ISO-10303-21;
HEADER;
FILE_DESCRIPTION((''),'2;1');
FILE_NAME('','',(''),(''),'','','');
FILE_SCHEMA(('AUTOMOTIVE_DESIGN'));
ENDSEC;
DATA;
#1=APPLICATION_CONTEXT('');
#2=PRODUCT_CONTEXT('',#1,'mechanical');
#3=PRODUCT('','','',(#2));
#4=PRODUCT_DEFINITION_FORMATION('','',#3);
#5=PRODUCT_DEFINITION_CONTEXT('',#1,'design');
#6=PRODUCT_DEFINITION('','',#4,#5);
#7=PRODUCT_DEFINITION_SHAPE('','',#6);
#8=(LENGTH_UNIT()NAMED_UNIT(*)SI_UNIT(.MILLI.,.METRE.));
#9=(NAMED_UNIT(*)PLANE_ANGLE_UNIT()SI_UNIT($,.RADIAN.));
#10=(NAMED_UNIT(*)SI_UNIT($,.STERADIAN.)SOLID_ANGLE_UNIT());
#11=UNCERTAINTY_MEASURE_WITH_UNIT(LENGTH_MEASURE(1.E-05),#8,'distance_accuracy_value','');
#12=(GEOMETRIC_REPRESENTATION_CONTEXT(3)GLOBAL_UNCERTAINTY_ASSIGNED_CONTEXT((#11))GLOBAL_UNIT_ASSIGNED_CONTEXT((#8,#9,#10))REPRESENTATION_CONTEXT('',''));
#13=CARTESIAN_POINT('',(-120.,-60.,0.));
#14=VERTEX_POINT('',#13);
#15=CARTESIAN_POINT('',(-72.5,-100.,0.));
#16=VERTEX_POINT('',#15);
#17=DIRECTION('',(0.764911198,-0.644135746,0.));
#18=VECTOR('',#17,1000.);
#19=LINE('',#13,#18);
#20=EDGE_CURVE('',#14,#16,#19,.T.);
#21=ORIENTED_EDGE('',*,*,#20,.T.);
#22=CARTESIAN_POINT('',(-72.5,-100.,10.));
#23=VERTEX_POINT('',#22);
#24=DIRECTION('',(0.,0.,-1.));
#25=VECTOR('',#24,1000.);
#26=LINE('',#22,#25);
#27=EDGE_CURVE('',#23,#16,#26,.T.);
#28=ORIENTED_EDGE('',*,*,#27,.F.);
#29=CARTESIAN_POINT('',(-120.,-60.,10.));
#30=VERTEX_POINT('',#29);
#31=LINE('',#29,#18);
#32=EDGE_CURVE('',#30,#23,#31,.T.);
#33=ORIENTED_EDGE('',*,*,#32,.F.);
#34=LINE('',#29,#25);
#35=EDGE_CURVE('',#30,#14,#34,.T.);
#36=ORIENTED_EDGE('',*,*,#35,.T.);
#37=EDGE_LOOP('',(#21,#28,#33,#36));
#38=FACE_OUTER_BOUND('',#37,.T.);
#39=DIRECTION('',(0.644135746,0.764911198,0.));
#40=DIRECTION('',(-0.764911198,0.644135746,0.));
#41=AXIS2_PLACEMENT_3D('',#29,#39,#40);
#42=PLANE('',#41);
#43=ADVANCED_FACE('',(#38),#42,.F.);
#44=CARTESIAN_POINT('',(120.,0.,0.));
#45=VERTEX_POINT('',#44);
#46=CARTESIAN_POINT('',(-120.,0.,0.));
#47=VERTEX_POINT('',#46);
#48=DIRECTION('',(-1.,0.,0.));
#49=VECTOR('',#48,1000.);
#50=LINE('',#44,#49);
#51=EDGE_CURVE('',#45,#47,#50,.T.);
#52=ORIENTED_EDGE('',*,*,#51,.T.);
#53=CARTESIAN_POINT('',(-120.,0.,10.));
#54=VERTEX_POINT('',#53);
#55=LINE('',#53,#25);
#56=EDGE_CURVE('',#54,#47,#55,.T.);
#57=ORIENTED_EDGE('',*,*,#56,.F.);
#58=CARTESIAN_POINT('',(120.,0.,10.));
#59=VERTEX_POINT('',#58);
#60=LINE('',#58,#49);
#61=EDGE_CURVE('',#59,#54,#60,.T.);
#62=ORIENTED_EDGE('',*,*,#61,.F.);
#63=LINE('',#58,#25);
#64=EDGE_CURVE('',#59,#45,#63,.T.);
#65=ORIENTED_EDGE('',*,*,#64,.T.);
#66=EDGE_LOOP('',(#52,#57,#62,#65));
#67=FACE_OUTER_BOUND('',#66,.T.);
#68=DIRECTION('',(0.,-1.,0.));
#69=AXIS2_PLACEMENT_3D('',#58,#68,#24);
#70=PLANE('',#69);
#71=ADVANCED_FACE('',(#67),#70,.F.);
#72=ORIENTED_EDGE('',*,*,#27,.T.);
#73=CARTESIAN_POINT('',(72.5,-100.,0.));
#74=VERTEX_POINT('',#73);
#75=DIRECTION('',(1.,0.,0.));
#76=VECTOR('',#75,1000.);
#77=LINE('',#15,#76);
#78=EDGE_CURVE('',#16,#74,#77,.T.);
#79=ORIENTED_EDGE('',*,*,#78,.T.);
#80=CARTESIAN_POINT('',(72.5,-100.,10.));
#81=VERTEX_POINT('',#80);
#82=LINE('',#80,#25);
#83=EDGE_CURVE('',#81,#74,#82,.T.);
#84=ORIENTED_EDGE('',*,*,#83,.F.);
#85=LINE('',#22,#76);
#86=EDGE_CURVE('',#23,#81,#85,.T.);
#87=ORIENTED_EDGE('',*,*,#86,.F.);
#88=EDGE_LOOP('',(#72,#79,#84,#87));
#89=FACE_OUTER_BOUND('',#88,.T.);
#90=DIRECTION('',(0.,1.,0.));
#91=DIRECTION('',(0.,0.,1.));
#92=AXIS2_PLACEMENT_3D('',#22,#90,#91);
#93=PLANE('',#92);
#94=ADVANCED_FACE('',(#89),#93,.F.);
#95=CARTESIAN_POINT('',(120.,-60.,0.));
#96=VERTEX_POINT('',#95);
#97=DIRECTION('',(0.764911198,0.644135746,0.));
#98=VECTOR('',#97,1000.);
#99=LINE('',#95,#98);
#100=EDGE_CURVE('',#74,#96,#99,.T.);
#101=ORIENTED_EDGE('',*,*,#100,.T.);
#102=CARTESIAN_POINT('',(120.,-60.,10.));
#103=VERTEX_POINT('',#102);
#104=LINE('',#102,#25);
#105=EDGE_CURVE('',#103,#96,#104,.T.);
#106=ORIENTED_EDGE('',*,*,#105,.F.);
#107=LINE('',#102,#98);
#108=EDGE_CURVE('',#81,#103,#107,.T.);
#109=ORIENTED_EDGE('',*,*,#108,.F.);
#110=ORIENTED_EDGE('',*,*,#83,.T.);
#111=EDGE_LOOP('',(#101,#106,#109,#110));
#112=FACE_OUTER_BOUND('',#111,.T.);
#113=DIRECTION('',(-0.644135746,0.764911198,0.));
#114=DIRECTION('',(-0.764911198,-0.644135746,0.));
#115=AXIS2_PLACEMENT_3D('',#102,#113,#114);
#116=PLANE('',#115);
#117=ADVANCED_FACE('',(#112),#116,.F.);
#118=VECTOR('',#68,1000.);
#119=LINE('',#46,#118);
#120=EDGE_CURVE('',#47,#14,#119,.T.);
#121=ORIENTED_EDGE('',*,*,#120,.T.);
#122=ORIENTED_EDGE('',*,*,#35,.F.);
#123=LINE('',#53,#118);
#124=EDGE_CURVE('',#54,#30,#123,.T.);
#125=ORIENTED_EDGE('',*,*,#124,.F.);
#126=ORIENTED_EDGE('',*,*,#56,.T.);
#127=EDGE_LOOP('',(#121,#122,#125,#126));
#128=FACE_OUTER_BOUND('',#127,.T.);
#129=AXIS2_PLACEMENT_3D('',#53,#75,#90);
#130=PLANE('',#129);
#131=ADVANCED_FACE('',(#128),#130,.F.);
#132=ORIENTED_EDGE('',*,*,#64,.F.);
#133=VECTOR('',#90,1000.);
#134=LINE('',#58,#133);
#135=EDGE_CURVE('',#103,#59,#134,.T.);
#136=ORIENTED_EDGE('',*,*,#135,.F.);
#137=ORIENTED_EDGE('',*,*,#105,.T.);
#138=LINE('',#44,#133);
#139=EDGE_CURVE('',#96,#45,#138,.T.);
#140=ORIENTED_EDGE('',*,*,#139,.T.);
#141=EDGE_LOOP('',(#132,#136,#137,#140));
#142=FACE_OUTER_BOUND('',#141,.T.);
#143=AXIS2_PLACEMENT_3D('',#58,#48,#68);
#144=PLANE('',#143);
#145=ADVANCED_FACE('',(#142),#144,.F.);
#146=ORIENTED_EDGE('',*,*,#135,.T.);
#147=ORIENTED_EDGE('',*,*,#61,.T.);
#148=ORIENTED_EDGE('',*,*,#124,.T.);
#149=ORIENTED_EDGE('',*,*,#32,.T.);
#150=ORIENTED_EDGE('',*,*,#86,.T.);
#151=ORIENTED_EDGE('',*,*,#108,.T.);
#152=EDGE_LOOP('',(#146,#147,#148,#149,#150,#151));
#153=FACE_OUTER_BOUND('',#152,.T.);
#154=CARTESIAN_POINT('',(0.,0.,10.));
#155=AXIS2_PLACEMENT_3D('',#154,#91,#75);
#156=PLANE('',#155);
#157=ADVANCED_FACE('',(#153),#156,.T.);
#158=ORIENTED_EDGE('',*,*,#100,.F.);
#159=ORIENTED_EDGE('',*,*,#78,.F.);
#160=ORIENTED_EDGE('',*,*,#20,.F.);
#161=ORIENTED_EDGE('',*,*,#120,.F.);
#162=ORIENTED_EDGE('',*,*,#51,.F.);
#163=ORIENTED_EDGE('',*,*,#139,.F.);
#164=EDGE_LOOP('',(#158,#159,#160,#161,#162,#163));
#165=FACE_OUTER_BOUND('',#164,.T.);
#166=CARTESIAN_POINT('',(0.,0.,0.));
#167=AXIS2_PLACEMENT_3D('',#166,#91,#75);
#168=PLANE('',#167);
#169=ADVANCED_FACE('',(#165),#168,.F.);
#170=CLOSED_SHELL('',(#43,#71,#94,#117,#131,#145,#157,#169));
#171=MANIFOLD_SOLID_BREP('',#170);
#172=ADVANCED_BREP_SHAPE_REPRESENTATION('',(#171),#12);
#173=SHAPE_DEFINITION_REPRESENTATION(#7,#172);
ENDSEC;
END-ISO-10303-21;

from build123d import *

# Parameters (mm, degrees)
EXTRUDE_1_DEPTH = 10


with BuildPart() as part:
    # 草图1 → 凸台-拉伸1 (new body)
    with BuildSketch(Plane.XY):
        Polygon((120, 0), (-120, 0), (-120, -60), (-72.5, -100), (72.5, -100), (120, -60), align=None)
    extrude(amount=EXTRUDE_1_DEPTH)


solid = part.part
